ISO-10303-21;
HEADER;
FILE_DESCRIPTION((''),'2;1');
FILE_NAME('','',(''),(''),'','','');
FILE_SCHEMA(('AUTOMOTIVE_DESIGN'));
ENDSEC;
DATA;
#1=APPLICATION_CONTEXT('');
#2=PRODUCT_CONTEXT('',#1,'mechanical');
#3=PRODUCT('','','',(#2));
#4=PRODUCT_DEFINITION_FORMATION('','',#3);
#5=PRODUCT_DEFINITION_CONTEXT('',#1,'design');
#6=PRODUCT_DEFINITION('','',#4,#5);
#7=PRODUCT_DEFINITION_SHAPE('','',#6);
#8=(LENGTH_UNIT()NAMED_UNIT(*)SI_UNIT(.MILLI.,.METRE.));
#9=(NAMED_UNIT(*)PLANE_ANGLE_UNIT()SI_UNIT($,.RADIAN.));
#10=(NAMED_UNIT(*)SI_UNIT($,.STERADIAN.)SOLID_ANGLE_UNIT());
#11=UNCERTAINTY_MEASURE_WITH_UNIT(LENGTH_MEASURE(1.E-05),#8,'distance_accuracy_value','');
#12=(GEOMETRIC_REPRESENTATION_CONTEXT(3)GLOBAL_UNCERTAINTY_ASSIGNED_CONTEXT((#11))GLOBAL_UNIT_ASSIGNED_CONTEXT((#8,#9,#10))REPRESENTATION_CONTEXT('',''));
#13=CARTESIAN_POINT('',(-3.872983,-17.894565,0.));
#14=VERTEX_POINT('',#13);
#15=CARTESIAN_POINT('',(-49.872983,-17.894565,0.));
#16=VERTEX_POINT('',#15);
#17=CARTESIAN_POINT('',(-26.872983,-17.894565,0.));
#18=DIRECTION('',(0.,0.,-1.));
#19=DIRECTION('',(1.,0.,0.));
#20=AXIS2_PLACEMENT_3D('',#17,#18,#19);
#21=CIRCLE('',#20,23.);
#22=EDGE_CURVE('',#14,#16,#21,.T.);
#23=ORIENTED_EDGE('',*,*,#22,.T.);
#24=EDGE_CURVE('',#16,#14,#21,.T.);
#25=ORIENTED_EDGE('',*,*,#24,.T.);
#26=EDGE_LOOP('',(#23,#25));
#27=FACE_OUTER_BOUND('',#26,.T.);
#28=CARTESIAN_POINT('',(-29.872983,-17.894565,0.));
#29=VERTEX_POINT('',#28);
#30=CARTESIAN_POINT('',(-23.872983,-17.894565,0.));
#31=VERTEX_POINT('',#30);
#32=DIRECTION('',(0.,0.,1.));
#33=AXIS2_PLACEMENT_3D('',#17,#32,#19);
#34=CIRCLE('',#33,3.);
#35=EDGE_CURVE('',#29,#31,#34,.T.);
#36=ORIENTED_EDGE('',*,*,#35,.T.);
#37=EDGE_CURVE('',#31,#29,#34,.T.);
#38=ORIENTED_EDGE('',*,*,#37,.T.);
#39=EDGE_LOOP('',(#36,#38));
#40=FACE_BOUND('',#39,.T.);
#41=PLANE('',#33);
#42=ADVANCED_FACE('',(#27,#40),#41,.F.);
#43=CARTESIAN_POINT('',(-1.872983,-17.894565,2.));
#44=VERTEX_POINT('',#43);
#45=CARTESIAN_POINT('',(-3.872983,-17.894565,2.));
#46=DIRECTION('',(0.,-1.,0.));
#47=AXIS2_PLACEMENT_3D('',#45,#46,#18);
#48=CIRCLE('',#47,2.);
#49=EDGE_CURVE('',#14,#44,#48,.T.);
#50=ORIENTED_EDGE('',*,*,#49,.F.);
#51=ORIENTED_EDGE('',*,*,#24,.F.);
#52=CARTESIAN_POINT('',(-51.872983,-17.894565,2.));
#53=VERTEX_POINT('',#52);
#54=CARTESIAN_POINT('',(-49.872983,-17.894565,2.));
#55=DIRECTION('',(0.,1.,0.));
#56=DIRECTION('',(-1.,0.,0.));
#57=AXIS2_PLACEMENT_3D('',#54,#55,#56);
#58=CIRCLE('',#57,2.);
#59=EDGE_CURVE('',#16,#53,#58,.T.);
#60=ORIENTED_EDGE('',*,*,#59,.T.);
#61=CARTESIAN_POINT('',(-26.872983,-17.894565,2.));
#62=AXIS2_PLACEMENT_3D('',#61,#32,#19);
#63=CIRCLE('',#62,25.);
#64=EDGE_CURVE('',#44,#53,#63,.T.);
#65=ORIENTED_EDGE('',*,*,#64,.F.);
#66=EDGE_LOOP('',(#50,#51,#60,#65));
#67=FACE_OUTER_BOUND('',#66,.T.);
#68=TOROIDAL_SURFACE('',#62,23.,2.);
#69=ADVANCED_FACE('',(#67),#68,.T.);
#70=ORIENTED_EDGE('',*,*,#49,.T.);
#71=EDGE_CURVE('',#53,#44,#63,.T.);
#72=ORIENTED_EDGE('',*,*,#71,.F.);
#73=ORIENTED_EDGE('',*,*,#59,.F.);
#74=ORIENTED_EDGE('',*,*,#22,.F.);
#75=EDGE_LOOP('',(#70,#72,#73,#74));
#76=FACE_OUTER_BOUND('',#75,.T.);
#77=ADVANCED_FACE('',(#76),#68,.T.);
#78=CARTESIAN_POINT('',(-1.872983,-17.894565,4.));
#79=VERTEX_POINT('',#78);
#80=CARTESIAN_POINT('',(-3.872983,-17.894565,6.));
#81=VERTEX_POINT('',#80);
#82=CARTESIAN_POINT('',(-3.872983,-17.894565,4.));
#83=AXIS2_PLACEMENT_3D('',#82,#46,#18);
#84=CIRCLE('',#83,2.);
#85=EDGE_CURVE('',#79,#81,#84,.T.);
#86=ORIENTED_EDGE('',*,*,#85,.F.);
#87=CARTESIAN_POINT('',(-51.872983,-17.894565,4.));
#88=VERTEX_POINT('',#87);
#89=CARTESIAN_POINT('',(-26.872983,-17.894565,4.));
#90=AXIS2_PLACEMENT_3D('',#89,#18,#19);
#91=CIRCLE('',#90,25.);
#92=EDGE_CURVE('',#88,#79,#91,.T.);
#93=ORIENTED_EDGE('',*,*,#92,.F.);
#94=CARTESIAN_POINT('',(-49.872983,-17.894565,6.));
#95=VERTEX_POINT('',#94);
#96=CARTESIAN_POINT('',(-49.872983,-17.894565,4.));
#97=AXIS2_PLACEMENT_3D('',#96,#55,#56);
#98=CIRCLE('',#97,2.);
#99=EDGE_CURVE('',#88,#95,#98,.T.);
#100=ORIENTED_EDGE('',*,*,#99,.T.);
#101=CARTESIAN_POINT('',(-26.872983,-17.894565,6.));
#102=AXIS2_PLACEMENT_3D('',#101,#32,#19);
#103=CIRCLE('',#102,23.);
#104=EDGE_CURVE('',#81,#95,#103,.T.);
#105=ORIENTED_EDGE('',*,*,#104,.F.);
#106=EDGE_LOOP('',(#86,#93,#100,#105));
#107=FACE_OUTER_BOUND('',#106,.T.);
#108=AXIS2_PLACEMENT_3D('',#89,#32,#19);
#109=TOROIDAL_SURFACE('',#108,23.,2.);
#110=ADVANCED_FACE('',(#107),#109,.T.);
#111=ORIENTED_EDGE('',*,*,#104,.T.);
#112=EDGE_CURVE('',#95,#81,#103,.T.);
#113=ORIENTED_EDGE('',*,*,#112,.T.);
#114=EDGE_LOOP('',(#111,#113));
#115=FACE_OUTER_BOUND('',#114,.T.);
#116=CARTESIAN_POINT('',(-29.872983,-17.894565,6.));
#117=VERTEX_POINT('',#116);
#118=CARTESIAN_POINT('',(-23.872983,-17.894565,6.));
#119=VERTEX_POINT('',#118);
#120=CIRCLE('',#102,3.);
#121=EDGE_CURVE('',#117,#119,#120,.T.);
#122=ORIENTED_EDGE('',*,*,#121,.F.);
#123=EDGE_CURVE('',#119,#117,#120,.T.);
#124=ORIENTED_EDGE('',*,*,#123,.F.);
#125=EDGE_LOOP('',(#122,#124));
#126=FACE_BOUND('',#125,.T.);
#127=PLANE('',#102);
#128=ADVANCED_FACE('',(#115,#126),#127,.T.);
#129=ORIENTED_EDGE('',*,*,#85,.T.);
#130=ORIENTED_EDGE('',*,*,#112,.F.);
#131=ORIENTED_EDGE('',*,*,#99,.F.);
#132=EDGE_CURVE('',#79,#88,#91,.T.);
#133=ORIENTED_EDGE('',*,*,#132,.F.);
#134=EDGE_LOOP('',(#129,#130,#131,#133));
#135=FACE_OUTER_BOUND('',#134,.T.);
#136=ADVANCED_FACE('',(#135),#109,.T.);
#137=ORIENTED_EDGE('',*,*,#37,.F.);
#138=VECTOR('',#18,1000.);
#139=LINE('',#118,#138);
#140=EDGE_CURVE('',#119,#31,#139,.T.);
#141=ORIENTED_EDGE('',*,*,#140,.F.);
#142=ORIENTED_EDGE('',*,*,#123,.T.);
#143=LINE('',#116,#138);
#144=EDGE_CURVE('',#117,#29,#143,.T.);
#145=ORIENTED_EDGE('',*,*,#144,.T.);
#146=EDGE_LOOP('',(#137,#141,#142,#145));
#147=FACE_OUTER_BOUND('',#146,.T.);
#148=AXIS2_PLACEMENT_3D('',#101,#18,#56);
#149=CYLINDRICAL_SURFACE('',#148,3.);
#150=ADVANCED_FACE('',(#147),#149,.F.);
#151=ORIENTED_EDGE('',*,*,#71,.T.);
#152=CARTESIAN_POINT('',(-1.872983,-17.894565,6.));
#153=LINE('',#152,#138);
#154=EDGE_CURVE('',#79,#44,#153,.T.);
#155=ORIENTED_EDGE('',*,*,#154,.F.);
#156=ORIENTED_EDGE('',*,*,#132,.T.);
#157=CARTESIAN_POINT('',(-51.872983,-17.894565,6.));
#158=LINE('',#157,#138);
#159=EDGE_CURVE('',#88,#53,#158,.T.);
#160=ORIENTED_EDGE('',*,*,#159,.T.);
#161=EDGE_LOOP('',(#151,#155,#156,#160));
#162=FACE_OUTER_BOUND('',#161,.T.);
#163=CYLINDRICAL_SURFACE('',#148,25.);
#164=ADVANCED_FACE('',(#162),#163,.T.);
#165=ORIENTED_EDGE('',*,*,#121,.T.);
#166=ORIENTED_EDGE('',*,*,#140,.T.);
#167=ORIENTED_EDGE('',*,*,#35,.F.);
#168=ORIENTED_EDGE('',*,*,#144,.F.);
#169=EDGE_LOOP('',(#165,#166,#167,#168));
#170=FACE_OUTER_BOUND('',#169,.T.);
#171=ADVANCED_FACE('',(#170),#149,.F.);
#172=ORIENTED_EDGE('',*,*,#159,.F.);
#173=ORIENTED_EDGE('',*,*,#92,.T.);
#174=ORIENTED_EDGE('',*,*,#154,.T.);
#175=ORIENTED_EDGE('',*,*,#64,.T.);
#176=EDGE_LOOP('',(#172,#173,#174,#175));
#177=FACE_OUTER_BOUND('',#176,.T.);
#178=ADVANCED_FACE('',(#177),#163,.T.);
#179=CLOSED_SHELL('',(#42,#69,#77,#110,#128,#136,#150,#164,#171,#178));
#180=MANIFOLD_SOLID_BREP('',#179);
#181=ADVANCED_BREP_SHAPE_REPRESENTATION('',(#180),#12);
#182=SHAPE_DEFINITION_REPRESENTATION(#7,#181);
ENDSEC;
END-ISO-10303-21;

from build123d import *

# Parameters (mm, degrees)
MODEL_R             = 25
MODEL_R_2           = 3
BOSS_EXTRUDE1_DEPTH = 6
FILLET1_R           = 2


with BuildPart() as part:
    # Model → Boss-Extrude1 (new body)
    with BuildSketch(Plane.XY):
        with Locations((-26.872983371, -17.894565392)):
            Circle(MODEL_R)
        with Locations((-26.872983371, -17.894565392)):
            Circle(MODEL_R_2, mode=Mode.SUBTRACT)
    extrude(amount=BOSS_EXTRUDE1_DEPTH)

    # Fillet1
    fillet1_edges = [part.edges().sort_by_distance(p)[0] for p in [
        (-51.872983371, -17.894565392, 0),
        (-51.872983371, -17.894565392, 6),
    ]]
    fillet(fillet1_edges, radius=FILLET1_R)


solid = part.part
